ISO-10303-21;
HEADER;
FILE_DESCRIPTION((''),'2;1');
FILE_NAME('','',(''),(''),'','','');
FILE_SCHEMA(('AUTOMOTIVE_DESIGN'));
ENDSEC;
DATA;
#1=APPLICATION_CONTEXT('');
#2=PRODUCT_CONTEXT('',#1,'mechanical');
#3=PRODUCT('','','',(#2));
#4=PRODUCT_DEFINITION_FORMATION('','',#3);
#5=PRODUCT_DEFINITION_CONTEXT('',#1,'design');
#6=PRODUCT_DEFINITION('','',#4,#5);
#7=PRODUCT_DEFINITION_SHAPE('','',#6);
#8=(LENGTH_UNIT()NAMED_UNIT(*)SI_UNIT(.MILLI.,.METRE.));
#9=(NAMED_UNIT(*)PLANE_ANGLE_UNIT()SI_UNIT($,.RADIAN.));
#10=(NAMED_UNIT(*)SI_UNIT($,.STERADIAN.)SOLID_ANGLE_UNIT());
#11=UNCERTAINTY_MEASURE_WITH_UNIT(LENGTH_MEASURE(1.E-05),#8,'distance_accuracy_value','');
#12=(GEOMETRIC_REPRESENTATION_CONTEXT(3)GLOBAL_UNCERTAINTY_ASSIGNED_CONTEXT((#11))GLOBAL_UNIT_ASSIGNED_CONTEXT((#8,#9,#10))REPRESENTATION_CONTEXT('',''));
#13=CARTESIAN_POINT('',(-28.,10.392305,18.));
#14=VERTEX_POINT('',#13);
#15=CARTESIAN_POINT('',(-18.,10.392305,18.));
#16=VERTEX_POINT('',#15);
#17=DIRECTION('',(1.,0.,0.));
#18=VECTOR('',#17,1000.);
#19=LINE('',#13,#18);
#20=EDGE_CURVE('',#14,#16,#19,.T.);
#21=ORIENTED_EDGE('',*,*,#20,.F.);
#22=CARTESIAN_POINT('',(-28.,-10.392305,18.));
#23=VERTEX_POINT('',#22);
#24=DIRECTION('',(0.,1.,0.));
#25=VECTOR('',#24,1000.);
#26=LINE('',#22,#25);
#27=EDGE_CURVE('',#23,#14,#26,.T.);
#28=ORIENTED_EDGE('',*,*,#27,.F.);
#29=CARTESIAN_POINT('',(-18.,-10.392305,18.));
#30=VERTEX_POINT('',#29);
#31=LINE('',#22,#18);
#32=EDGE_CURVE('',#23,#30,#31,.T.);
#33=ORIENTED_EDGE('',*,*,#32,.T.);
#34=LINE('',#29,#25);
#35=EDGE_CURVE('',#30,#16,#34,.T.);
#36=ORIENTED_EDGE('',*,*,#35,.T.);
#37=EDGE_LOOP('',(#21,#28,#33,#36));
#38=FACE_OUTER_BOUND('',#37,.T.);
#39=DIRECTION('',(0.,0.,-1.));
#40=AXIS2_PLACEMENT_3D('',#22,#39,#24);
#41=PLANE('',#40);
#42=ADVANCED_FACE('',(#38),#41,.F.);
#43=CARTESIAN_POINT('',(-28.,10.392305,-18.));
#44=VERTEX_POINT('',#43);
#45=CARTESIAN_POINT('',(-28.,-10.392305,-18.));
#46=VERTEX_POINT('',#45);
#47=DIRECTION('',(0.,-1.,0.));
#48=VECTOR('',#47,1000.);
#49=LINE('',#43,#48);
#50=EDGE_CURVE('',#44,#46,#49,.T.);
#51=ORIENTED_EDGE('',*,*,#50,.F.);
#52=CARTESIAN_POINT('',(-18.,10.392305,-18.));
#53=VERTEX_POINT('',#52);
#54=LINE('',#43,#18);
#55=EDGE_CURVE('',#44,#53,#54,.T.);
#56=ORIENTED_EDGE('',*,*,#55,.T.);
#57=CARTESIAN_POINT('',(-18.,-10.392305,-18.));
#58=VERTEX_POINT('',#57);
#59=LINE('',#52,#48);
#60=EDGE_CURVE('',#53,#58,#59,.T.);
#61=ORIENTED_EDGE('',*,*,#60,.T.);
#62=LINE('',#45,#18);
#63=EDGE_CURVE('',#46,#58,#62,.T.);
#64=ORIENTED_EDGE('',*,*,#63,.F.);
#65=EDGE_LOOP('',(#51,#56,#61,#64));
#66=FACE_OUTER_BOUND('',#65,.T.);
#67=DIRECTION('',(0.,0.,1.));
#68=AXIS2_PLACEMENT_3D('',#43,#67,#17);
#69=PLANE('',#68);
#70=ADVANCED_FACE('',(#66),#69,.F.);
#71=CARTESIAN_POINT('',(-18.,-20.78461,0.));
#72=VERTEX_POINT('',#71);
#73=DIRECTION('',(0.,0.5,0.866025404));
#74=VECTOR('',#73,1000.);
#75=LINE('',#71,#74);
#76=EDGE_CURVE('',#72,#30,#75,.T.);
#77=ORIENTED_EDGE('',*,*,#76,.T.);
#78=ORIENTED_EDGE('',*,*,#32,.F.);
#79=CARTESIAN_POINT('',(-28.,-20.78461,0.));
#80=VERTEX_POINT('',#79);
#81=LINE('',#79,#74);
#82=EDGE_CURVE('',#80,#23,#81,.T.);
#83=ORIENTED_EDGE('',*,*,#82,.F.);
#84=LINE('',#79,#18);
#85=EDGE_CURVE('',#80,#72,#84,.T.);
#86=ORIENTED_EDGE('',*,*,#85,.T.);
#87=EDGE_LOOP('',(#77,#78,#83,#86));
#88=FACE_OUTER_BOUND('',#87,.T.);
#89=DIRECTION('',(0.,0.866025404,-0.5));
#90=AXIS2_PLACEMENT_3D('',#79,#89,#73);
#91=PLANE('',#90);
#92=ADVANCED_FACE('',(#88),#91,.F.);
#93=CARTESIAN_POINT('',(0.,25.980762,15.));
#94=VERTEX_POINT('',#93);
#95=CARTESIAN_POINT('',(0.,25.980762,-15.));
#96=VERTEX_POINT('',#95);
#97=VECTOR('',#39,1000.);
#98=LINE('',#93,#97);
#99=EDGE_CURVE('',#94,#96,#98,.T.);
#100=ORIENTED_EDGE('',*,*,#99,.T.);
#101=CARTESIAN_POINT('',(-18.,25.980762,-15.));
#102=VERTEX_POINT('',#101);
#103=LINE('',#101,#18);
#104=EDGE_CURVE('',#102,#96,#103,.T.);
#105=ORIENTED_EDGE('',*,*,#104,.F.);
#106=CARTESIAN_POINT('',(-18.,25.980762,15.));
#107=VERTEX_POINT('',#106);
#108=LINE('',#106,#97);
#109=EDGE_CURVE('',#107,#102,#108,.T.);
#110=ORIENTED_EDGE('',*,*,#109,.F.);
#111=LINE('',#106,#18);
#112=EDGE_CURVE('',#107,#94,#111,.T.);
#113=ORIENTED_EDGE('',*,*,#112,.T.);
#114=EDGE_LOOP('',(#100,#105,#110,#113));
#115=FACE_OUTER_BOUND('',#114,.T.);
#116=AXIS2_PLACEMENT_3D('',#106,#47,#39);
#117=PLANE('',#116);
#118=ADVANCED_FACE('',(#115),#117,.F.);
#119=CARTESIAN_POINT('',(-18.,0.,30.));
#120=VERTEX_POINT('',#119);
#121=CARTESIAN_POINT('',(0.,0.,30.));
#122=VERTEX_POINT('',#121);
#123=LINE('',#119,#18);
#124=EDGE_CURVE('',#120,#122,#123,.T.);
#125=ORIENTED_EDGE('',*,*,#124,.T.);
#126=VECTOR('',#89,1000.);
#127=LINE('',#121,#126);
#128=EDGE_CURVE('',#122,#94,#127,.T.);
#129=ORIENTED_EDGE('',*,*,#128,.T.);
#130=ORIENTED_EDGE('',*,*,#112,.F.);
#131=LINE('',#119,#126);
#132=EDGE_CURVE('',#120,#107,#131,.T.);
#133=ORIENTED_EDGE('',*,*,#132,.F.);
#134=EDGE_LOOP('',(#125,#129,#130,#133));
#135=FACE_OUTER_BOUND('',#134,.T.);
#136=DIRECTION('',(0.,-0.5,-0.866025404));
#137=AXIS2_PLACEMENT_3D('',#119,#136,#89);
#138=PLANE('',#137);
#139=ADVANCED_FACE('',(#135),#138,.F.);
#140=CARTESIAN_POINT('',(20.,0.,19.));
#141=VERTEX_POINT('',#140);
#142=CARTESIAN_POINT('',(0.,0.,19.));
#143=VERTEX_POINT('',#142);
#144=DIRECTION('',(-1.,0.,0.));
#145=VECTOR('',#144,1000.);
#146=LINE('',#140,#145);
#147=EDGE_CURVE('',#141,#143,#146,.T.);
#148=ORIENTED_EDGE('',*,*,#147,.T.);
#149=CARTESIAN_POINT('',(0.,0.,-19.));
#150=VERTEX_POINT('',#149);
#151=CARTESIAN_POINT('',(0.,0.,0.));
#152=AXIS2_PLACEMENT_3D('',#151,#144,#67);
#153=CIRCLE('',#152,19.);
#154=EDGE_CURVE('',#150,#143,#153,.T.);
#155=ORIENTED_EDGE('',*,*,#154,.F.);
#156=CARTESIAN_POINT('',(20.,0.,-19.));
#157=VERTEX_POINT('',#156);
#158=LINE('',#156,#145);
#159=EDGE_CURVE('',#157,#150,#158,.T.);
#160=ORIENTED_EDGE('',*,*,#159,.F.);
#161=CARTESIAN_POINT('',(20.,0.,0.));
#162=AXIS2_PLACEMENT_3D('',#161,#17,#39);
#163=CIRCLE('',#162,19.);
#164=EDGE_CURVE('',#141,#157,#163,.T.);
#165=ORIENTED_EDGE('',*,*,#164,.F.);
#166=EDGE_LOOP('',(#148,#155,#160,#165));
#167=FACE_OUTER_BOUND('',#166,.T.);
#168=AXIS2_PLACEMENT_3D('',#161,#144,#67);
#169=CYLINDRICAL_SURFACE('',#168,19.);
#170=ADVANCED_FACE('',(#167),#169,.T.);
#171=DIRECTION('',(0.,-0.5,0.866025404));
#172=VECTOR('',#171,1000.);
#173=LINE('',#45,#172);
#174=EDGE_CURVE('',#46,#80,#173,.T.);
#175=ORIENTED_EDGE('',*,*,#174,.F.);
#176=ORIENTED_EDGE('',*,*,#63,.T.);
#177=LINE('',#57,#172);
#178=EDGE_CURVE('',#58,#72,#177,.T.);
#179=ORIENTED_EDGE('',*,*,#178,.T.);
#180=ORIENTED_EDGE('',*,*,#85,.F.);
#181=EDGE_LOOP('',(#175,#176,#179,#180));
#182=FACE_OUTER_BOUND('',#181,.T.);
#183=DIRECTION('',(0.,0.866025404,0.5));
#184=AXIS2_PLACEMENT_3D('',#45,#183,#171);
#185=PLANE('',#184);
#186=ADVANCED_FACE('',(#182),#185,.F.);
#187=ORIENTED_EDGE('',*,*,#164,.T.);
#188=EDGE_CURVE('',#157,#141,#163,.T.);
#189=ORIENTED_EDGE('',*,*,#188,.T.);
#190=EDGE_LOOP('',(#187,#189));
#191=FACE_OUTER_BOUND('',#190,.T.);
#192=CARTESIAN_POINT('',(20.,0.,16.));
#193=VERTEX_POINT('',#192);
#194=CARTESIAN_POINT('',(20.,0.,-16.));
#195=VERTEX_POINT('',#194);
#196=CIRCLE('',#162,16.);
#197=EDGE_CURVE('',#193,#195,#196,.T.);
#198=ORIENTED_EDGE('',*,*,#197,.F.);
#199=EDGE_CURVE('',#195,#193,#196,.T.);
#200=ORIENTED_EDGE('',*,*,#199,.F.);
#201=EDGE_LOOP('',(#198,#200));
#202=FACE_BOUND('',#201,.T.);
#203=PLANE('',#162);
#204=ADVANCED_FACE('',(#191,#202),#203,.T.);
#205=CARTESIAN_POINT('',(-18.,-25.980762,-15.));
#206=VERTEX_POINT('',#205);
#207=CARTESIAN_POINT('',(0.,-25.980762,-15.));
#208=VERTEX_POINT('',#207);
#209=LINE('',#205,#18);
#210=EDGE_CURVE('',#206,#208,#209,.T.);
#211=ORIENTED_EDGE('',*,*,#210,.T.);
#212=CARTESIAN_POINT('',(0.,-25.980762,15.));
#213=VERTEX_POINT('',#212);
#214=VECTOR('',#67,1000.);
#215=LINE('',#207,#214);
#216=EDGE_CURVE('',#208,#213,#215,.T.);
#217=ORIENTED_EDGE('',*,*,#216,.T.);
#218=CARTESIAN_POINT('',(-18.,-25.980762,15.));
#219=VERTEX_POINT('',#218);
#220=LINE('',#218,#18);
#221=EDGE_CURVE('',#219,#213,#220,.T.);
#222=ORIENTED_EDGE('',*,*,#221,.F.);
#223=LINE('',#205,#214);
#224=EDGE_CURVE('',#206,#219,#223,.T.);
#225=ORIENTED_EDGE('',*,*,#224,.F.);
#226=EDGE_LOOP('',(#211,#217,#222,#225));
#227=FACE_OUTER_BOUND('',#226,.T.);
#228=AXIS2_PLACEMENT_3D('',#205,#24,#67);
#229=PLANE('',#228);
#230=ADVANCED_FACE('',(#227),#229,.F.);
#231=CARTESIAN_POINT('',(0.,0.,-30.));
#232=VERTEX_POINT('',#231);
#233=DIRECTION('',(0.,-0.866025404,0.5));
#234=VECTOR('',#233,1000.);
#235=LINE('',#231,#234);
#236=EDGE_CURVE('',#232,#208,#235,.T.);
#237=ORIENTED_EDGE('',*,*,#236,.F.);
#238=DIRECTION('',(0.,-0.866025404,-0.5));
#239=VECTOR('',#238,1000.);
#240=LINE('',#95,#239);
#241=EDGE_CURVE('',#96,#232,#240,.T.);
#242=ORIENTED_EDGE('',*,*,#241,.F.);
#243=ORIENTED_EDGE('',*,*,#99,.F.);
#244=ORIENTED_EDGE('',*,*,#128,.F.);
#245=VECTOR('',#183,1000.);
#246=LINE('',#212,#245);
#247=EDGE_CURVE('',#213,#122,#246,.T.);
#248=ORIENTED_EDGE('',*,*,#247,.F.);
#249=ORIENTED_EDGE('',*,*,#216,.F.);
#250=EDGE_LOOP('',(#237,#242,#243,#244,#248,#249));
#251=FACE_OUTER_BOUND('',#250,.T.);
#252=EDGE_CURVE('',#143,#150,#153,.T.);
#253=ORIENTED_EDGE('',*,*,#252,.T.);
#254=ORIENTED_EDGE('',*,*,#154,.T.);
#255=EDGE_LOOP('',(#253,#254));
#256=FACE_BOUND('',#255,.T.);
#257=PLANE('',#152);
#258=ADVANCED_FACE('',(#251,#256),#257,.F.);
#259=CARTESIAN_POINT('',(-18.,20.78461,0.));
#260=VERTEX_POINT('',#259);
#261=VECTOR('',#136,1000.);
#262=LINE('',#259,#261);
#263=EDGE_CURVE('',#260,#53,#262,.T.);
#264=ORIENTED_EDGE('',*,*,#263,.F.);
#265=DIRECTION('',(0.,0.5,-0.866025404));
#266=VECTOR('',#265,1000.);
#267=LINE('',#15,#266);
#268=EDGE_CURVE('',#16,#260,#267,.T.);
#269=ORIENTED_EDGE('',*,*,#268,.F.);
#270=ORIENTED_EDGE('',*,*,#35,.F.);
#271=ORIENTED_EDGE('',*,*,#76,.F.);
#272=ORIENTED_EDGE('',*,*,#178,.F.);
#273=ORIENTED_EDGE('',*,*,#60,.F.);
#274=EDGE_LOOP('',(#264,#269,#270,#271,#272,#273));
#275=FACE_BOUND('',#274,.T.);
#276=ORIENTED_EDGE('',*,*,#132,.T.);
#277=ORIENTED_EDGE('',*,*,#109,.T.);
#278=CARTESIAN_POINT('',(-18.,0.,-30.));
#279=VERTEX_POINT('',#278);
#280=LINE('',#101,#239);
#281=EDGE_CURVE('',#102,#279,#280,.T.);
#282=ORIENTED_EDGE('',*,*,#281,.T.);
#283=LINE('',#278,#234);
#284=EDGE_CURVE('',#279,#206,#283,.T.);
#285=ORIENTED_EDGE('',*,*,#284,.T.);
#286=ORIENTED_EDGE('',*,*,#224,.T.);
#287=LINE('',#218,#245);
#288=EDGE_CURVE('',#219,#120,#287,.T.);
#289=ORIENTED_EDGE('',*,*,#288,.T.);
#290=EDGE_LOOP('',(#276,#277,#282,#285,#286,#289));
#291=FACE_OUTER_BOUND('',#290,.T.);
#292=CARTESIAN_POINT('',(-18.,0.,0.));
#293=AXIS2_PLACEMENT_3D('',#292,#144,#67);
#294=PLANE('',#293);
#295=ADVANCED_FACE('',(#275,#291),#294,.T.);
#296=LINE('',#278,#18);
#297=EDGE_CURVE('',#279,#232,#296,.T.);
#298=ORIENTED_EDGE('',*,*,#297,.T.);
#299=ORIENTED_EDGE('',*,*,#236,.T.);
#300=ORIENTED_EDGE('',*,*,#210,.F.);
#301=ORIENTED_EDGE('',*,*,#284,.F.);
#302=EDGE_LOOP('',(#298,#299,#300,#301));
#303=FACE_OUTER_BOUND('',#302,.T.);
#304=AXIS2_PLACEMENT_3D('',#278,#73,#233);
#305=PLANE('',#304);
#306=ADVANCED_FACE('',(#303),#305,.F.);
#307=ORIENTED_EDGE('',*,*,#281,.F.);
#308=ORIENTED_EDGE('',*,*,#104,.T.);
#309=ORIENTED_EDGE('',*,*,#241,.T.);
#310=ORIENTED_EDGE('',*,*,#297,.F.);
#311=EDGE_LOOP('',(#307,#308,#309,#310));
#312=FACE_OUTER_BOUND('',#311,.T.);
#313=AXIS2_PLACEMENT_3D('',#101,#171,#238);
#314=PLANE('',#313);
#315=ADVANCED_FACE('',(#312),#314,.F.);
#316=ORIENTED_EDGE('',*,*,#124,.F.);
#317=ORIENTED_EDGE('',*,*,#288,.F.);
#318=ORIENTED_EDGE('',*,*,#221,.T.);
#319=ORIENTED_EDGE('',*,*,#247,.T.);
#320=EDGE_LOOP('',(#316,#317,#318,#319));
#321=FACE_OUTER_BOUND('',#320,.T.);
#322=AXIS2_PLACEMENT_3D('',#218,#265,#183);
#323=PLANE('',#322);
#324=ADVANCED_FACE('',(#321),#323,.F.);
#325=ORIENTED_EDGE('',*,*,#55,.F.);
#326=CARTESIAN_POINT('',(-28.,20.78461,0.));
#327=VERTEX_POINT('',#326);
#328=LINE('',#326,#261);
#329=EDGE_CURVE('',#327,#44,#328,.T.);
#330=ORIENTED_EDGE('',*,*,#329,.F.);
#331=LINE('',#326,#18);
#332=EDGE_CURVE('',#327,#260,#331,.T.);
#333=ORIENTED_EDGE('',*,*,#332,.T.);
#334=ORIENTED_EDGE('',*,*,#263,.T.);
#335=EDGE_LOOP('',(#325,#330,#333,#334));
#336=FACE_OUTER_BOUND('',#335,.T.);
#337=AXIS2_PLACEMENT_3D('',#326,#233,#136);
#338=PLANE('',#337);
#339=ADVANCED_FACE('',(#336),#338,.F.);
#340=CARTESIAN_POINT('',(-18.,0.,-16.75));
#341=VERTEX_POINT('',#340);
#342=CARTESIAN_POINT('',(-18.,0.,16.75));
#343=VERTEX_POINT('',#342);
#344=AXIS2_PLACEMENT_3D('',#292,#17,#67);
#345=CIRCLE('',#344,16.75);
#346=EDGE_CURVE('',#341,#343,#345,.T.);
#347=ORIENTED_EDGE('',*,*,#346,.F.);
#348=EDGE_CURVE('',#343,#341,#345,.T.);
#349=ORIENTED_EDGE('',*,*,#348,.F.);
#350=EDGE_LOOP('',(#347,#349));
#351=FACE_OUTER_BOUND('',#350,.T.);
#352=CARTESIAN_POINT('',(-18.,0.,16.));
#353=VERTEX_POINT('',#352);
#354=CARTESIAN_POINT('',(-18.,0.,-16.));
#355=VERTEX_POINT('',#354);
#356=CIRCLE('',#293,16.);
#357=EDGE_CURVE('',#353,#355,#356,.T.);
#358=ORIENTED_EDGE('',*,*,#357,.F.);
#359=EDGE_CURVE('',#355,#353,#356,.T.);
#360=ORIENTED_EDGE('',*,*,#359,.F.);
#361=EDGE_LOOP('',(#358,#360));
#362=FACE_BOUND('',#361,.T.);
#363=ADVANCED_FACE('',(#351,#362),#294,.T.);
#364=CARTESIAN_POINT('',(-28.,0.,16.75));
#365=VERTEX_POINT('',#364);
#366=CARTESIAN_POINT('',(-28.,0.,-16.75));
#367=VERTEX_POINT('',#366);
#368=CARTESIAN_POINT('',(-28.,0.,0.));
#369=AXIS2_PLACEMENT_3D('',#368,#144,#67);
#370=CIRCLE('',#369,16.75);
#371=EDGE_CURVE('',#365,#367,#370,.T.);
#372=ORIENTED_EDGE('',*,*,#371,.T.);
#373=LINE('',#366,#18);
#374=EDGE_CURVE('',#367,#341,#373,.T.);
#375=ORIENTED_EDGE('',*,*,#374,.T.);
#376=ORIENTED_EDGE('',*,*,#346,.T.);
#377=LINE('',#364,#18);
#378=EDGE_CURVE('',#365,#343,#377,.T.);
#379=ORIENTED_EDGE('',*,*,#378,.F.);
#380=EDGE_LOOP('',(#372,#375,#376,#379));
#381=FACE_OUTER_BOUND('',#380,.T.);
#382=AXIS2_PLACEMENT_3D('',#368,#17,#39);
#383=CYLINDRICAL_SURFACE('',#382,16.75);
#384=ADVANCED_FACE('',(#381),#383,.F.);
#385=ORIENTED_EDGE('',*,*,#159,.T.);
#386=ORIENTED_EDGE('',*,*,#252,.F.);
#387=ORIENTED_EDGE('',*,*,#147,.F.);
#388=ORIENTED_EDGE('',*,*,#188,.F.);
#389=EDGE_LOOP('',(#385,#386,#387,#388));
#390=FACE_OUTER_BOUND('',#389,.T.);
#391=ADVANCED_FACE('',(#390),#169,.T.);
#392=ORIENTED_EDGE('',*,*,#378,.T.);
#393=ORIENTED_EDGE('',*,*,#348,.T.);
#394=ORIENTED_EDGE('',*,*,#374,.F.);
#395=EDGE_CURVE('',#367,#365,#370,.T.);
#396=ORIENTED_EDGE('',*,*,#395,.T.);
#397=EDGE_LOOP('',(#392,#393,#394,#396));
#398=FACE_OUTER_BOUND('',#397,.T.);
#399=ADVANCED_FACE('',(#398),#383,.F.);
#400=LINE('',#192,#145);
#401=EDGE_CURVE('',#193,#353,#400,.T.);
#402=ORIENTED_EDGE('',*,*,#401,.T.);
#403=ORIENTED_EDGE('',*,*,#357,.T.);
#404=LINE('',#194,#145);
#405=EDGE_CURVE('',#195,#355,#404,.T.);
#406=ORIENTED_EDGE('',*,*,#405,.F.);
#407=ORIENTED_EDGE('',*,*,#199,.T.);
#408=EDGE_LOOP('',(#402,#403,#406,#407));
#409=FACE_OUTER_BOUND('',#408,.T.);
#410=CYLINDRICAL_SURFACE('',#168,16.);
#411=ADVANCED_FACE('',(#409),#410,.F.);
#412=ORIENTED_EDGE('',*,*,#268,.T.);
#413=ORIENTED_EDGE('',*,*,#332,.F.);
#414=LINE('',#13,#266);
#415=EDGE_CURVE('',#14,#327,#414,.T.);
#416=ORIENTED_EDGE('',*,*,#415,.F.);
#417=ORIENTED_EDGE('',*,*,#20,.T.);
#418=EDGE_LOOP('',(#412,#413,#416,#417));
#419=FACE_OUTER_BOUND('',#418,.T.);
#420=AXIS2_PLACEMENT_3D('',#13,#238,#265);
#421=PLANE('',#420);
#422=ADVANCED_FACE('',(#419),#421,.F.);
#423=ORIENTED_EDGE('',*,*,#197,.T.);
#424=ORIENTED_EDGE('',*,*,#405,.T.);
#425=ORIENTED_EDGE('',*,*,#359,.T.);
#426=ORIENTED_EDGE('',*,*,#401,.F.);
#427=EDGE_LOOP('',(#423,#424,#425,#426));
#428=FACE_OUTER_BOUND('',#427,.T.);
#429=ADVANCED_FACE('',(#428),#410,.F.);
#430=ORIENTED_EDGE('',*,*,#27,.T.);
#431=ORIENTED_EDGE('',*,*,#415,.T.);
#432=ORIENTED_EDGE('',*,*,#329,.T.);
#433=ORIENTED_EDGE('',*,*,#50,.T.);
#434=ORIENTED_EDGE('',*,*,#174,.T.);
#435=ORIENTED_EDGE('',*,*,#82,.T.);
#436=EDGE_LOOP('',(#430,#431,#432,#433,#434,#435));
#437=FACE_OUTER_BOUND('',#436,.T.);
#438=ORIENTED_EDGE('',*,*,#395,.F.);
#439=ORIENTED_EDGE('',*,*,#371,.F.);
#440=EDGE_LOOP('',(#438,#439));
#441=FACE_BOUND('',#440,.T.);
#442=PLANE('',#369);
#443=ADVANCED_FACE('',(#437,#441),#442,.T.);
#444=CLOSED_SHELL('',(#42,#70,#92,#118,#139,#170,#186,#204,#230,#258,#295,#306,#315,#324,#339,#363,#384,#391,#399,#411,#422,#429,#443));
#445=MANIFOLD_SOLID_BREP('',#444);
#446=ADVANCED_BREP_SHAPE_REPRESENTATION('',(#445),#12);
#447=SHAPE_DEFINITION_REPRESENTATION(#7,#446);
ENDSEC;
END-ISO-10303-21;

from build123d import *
from build123d.topology import SkipClean

# Parameters (mm, degrees)
SKETCH_1_R        = 19
SKETCH_1_R_2      = 16
EXTRUDE_1_DEPTH   = 20
EXTRUDE_START     = 18
SKETCH_2_R        = 16
EXTRUDE_1_2_DEPTH = 18
SKETCH_3_R        = 16.75
EXTRUDE_2_DEPTH   = 10


with BuildPart() as part:
    # 草图1 → Extrude 1 (new body)
    with BuildSketch(Plane(origin=(0, 0, 0), x_dir=(0, 0, -1), z_dir=(1, 0, 0))):
        Circle(SKETCH_1_R)
        Circle(SKETCH_1_R_2, mode=Mode.SUBTRACT)
    extrude(amount=EXTRUDE_1_DEPTH)

    # 草图2 → Extrude 1 2 (add)
    with SkipClean():  # the faces are left unmerged after this step: merging them gives an invalid solid
        with BuildSketch(Plane.ZY.offset(EXTRUDE_START)):
            Polygon((30, 0), (15, 25.980762114), (-15, 25.980762114), (-30, 0), (-15, -25.980762114), (15, -25.980762114), align=None)
            Circle(SKETCH_2_R, mode=Mode.SUBTRACT)
        extrude(amount=-EXTRUDE_1_2_DEPTH)

    # 草图3 → 凸台-拉伸2 (add)
    with SkipClean():  # the faces are left unmerged after this step: merging them gives an invalid solid
        with BuildSketch(Plane.ZY.offset(18)):
            Polygon((0, 20.784609691), (-18, 10.392304845), (-18, -10.392304845), (0, -20.784609691), (18, -10.392304845), (18, 10.392304845), align=None)
            Circle(SKETCH_3_R, mode=Mode.SUBTRACT)
        extrude(amount=EXTRUDE_2_DEPTH)


solid = part.part
